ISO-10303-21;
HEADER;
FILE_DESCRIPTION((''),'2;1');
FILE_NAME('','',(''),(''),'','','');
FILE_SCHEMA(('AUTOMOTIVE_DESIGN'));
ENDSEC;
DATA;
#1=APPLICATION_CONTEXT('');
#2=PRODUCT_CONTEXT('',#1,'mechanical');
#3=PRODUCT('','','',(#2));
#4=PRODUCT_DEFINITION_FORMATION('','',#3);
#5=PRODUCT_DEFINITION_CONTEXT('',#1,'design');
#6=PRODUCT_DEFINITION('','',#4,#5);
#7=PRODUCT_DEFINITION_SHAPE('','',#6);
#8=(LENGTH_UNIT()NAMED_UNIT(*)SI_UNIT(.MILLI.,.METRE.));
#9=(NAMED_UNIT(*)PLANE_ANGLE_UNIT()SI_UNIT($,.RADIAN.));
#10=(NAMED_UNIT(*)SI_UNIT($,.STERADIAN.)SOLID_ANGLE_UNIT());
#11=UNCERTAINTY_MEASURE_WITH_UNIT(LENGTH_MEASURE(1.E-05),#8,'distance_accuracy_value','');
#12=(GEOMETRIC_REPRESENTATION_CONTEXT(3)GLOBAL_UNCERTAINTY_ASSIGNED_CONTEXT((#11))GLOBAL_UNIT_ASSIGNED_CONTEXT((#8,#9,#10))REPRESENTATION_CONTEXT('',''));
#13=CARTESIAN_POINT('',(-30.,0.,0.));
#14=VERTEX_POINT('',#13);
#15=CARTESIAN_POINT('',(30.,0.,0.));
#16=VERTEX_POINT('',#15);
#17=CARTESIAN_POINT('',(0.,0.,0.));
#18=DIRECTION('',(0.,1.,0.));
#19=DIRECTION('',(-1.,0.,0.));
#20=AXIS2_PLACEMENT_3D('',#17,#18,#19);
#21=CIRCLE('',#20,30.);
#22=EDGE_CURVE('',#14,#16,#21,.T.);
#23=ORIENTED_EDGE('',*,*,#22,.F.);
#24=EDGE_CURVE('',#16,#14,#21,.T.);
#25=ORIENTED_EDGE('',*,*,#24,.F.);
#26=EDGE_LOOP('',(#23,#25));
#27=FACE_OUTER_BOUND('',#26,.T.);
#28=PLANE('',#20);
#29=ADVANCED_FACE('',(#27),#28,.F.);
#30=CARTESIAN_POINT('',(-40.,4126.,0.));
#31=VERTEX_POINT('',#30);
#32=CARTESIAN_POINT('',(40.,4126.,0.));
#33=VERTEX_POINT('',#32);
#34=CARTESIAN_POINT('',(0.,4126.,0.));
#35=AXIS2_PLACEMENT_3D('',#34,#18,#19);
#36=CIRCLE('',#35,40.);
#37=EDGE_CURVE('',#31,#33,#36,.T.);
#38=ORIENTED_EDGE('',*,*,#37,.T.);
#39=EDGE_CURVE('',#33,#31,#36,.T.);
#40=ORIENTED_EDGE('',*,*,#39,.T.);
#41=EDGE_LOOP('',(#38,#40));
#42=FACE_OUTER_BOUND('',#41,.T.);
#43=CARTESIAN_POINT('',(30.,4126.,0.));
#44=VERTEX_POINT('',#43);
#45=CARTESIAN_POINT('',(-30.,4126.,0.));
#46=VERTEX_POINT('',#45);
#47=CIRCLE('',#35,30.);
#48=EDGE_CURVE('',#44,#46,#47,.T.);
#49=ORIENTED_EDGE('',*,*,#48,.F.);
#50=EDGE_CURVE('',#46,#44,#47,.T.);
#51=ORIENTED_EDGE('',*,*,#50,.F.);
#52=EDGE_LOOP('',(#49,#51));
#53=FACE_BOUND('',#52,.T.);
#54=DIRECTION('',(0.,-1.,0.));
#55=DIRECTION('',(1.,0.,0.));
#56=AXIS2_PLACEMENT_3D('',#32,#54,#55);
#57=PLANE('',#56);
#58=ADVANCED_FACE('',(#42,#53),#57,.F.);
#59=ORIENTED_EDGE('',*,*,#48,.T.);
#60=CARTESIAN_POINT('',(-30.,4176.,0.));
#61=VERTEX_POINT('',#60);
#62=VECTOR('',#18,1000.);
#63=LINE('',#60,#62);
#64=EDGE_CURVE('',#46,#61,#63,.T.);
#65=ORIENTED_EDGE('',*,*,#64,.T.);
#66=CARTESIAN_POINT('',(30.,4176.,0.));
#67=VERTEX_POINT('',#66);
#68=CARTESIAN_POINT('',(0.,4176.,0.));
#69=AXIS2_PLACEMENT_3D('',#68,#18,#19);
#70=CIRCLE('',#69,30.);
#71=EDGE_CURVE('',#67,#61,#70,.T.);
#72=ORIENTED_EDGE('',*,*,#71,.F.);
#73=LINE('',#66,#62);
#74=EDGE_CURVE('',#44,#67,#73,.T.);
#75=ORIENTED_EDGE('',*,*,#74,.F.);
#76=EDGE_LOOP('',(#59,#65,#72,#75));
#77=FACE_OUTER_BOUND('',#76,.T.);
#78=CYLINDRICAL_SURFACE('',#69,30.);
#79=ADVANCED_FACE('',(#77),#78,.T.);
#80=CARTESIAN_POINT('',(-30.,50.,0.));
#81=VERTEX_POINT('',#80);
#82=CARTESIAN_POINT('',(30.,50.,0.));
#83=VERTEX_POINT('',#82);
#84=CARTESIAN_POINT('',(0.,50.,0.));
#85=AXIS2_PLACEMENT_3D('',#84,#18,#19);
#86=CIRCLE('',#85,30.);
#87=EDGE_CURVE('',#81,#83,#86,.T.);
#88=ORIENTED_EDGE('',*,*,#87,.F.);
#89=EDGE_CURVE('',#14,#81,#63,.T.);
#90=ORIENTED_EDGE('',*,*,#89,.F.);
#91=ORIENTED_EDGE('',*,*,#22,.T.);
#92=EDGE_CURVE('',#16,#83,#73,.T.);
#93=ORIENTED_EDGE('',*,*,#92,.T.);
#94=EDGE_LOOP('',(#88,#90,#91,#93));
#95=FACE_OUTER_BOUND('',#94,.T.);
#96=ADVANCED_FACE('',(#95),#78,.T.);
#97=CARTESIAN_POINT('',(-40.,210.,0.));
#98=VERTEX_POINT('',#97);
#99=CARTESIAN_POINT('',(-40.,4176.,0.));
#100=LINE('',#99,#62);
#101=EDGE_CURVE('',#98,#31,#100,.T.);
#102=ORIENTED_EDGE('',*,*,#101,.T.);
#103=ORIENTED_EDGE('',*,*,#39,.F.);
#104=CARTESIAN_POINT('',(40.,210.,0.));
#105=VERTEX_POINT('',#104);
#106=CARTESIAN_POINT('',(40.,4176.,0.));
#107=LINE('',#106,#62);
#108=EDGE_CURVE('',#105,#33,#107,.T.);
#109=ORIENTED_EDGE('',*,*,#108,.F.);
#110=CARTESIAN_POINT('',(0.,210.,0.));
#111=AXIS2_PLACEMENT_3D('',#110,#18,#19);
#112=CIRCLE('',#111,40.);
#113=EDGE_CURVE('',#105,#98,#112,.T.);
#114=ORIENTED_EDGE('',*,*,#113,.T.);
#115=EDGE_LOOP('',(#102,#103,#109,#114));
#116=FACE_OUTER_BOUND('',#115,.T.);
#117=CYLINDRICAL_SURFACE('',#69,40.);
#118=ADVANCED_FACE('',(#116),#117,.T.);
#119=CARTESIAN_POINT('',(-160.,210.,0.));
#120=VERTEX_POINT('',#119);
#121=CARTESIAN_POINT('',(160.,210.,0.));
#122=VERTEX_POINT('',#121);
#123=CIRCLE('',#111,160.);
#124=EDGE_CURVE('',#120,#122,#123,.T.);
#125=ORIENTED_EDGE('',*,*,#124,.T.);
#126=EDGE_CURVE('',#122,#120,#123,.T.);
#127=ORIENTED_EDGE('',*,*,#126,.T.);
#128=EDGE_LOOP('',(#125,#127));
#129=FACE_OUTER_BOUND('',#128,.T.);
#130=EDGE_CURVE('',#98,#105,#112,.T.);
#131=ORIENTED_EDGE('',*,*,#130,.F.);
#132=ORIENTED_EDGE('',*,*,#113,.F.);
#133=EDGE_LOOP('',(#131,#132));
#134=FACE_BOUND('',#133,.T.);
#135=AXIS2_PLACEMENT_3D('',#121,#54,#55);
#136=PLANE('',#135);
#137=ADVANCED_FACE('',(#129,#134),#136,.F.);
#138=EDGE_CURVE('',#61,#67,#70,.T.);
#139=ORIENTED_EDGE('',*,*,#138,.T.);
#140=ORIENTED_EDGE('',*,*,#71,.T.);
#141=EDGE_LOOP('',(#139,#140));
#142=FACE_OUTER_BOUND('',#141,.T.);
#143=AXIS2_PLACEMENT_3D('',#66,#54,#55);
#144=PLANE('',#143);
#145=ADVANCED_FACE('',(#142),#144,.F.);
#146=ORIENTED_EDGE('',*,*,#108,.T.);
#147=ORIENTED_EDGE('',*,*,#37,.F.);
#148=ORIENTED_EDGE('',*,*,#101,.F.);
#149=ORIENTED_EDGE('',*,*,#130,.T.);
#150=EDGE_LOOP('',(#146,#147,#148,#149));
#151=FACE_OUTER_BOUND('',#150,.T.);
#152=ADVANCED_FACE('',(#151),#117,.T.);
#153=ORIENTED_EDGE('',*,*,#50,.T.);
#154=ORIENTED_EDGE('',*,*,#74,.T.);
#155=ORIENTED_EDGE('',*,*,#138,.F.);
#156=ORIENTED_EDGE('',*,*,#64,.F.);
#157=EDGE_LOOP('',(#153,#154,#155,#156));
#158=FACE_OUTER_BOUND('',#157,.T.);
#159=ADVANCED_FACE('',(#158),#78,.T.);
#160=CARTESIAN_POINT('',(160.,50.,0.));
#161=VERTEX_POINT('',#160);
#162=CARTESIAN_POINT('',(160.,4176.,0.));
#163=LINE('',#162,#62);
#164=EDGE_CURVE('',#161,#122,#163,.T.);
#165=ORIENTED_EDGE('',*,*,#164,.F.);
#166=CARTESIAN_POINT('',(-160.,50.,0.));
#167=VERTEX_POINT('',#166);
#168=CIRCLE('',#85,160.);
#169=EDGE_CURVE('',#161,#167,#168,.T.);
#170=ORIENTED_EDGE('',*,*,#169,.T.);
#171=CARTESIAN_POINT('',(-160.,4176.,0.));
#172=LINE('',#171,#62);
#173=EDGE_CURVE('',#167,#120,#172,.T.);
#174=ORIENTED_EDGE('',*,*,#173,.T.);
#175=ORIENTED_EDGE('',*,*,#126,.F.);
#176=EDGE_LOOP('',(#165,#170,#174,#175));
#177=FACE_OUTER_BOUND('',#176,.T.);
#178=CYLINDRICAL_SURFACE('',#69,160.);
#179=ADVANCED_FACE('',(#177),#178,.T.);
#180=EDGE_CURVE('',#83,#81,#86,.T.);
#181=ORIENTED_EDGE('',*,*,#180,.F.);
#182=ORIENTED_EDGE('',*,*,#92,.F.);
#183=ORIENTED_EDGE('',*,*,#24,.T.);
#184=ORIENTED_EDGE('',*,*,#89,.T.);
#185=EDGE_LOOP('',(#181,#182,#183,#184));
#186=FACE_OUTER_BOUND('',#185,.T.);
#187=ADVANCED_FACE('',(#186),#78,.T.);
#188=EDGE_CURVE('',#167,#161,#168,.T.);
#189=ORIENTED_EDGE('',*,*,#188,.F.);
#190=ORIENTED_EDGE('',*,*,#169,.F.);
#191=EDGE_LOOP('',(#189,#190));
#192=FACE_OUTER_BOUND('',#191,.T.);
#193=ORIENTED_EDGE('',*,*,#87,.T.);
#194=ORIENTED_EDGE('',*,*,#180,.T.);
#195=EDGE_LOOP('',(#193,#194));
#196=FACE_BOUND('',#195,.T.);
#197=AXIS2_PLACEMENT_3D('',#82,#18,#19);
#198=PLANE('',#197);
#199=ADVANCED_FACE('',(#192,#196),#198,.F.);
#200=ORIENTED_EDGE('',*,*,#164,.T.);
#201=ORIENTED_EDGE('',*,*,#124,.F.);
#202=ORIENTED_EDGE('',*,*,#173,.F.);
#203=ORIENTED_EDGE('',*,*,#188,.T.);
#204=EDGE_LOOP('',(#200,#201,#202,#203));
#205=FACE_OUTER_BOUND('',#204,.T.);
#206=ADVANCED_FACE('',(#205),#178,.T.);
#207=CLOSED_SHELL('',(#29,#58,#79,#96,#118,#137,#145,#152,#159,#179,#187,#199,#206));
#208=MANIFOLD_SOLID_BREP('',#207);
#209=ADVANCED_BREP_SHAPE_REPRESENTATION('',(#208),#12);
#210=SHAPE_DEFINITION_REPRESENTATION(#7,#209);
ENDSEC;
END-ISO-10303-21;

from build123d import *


with BuildPart() as part:
    # Sketch1 → Revolve1 (revolve)
    with BuildSketch(Plane.XY, mode=Mode.PRIVATE) as revolve1_sk:
        Polygon((0, 0), (30, 0), (30, 50), (160, 50), (160, 210), (40, 210), (40, 4126), (30, 4126), (30, 4176), (0, 4176), align=None)
    revolve(revolve1_sk.sketch.rotate(Axis((0, 4176, 0), (0, -1, 0)), 180), axis=Axis((0, 4176, 0), (0, -1, 0)))


solid = part.part
